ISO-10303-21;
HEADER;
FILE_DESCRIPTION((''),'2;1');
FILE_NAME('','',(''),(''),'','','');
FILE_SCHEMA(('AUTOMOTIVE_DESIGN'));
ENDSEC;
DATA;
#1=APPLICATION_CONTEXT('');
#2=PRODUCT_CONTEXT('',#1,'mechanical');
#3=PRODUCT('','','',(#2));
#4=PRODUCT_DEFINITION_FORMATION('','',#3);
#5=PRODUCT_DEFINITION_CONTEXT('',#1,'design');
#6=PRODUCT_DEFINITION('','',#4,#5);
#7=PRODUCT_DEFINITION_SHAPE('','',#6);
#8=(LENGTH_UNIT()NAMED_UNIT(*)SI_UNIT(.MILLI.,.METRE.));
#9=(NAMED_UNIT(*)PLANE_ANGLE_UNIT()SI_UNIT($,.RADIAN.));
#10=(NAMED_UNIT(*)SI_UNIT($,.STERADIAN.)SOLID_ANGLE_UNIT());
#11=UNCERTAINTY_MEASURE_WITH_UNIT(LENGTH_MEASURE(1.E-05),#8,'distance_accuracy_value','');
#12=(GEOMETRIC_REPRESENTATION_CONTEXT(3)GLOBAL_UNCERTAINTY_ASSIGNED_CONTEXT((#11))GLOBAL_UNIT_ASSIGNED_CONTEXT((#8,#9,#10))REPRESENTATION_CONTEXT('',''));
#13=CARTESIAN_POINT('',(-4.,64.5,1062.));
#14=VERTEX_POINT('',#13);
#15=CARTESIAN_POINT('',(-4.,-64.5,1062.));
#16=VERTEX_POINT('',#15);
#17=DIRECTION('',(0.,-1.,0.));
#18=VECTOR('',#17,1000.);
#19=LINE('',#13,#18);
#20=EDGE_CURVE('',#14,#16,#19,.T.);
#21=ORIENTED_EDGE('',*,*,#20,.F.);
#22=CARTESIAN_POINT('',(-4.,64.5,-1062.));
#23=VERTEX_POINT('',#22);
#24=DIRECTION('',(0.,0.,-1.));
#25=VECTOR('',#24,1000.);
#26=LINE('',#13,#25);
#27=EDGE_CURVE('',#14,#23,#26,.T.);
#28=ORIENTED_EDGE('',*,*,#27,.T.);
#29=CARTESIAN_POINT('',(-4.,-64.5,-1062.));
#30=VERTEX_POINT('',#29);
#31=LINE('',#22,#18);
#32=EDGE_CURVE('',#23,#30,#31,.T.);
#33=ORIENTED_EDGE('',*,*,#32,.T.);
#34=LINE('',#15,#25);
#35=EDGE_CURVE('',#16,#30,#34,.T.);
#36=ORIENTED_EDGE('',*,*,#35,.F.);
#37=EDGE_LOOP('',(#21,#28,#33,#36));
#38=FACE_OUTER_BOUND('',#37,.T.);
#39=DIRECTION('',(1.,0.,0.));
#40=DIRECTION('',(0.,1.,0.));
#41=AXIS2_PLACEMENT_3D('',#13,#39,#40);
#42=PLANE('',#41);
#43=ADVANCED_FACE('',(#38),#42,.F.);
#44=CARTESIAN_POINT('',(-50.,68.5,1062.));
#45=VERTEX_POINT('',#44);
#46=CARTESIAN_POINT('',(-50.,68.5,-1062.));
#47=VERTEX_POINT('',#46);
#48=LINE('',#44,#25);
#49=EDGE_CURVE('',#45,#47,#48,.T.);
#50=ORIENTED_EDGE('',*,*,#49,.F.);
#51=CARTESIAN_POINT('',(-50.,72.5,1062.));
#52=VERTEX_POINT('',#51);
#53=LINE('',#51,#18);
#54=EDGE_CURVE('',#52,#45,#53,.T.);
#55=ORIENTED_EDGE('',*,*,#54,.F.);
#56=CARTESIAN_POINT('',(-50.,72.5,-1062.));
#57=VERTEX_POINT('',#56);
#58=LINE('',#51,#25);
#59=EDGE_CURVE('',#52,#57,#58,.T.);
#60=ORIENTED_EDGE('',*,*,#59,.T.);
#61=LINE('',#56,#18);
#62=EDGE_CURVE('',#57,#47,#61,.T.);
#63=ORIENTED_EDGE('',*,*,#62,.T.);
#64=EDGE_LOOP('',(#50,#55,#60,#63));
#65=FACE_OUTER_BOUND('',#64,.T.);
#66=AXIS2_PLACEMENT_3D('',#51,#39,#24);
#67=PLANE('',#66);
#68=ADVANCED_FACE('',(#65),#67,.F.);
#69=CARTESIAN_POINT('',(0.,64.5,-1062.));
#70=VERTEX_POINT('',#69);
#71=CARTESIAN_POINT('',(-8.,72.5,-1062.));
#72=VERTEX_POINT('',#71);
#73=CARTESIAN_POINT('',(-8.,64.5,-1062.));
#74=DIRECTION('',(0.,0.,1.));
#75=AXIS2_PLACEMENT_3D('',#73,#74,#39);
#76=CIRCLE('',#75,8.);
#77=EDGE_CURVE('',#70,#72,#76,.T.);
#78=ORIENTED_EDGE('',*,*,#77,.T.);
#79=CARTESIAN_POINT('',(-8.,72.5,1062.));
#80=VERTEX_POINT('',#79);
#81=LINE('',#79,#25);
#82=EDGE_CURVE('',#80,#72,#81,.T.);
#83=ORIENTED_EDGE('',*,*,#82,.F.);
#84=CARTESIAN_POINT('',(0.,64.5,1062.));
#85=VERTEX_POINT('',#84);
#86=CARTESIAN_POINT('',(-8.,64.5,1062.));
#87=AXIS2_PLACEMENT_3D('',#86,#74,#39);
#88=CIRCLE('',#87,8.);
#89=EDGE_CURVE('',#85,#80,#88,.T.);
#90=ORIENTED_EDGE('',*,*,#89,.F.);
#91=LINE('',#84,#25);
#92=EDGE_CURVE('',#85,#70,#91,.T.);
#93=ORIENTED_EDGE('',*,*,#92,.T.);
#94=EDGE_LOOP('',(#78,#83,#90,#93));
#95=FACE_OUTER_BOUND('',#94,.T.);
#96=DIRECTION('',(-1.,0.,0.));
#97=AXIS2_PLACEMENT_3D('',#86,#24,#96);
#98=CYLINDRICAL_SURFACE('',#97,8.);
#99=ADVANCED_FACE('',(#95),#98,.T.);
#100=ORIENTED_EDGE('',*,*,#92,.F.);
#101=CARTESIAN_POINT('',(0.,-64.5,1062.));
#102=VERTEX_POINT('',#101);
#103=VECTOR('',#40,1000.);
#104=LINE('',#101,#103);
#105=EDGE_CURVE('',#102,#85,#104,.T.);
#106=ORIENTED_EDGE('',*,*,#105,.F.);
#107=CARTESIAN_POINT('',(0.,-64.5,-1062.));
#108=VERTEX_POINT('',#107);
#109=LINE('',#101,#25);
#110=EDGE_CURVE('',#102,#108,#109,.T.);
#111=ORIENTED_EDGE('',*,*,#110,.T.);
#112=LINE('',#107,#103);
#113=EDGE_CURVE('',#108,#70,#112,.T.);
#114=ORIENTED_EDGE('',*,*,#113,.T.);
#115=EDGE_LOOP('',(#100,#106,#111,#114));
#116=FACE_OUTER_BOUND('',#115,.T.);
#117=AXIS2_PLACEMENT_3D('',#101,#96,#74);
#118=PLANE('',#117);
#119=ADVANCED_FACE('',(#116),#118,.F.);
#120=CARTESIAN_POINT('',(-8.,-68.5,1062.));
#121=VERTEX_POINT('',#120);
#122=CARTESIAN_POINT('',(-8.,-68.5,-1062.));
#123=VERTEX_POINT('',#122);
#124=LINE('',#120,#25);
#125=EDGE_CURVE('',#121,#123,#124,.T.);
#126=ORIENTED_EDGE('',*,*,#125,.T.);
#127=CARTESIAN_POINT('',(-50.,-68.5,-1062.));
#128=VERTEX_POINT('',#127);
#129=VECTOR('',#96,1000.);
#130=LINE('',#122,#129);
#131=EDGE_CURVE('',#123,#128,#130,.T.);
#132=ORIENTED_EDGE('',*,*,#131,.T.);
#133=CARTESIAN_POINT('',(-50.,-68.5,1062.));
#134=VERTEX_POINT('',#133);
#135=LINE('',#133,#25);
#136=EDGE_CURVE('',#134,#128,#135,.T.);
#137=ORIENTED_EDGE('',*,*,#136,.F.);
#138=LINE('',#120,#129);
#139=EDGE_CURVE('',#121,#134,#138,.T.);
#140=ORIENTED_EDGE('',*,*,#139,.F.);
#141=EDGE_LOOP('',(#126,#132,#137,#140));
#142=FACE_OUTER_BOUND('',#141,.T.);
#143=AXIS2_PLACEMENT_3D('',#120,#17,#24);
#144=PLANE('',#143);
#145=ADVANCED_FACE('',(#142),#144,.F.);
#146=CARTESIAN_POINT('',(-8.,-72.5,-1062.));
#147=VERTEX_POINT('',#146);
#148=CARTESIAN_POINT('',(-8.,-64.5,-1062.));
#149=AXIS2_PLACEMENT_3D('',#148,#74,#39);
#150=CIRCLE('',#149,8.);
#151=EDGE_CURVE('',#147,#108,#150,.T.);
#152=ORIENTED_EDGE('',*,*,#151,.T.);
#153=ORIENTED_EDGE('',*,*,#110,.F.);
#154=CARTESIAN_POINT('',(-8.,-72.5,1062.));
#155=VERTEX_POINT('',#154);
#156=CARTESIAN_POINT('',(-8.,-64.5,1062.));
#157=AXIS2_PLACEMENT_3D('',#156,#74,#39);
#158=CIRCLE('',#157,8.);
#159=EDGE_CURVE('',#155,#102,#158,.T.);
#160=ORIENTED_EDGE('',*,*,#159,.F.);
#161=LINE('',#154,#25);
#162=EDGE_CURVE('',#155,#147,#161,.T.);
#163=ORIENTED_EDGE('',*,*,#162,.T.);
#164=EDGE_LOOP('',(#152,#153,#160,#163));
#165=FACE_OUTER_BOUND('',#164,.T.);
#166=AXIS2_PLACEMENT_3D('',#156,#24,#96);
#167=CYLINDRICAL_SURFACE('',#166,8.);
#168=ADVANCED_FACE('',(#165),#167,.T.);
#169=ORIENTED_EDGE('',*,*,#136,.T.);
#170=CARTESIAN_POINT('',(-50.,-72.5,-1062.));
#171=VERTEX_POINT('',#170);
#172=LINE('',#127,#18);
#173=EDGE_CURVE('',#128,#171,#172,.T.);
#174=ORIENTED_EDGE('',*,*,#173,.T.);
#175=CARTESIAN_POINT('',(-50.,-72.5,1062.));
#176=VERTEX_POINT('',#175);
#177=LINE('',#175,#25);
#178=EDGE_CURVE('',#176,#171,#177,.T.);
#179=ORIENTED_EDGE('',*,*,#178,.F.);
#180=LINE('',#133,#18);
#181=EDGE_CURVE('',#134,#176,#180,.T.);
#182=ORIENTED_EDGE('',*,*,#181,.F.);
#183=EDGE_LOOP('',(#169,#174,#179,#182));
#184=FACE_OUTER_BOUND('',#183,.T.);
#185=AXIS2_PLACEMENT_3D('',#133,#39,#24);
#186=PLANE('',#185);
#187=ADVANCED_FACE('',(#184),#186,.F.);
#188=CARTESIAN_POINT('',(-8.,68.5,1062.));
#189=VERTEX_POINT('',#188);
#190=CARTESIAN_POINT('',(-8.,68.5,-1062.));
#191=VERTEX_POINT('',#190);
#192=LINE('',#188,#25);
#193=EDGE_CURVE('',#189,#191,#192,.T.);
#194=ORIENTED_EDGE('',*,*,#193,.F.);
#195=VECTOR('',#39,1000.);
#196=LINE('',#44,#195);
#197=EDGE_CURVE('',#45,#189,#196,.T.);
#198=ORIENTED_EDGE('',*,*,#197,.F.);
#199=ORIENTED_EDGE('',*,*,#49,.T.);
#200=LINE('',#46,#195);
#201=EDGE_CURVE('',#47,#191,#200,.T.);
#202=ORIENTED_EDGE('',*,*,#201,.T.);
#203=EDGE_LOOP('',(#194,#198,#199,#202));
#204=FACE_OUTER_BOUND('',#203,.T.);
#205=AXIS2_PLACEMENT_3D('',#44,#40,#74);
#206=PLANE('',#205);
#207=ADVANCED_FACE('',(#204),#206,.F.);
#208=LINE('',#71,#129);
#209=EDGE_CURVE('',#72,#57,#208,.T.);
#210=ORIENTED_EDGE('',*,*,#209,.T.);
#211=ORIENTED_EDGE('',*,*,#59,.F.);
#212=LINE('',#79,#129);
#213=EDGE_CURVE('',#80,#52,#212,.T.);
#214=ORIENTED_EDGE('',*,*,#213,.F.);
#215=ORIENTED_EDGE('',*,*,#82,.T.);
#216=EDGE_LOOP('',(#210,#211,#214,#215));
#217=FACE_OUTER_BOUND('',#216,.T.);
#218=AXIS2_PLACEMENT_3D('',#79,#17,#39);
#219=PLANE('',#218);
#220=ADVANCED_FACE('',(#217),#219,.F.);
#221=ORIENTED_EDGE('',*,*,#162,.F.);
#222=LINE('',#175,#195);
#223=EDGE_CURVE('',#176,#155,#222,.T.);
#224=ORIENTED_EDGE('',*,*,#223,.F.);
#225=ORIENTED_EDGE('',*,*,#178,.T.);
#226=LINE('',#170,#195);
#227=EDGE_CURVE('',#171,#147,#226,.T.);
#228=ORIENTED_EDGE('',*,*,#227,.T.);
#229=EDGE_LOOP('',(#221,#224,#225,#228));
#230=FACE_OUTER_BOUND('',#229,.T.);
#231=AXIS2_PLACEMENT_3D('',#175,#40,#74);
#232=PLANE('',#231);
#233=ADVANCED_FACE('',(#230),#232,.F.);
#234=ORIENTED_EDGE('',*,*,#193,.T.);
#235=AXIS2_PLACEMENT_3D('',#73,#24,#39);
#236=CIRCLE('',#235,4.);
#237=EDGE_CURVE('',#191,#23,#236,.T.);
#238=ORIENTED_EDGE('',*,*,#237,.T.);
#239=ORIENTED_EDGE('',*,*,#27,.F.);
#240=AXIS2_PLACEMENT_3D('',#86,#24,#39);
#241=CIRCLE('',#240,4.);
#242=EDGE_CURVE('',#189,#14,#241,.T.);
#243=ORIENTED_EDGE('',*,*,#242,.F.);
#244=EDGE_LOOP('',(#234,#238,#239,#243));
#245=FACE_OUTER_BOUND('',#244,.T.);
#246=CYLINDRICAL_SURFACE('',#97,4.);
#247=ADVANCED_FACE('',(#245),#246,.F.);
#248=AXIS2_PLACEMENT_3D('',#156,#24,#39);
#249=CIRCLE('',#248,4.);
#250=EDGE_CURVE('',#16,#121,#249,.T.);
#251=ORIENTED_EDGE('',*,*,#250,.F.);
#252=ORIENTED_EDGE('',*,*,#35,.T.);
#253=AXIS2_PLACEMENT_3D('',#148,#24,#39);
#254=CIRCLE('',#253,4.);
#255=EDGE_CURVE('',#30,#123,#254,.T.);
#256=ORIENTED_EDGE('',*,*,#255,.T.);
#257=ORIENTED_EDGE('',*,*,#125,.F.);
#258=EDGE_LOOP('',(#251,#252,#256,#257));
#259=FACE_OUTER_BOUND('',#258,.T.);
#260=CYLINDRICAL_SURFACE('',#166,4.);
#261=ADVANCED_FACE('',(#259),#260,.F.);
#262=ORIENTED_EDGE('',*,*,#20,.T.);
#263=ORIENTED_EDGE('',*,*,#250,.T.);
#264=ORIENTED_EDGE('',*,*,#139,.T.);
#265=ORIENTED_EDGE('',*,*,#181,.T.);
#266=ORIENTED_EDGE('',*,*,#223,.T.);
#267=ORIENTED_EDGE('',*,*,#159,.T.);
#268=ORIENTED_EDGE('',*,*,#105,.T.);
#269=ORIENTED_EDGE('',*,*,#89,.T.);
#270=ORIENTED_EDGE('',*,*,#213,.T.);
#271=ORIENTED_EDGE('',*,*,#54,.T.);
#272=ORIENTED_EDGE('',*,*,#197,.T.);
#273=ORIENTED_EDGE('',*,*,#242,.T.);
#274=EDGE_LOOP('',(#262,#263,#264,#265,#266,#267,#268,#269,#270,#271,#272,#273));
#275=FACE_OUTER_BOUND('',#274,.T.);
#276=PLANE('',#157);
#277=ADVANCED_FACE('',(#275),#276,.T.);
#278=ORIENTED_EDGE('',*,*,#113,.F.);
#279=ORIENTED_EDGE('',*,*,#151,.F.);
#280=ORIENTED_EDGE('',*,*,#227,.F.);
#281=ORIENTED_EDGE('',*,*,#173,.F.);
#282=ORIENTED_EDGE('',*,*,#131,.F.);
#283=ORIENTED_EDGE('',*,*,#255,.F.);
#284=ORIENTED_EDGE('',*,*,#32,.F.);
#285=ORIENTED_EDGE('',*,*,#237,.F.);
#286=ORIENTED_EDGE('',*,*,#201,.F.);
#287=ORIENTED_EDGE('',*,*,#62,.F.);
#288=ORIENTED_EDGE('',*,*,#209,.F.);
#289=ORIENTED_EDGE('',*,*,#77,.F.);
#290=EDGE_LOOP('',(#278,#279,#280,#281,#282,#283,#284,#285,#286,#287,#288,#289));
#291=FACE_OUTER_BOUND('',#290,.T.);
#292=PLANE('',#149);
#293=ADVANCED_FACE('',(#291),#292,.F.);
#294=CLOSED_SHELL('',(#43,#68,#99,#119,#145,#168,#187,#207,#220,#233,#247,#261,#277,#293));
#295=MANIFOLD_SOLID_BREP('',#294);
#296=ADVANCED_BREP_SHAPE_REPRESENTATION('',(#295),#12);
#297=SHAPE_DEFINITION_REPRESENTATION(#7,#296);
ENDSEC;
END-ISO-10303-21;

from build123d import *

# Parameters (mm, degrees)
BOSS_EXTRUDE1_DEPTH = 1062


with BuildPart() as part:
    # Sketch1 → Boss-Extrude1 (new, symmetric)
    with BuildSketch(Plane.XY):
        with BuildLine():
            Line((-50, -72.5), (-8, -72.5))
            ThreePointArc((-8, -72.5), (-2.343145751, -70.156854249), (0, -64.5))
            Line((0, -64.5), (0, 64.5))
            ThreePointArc((0, 64.5), (-2.343145751, 70.156854249), (-8, 72.5))
            Line((-8, 72.5), (-50, 72.5))
            Line((-50, 72.5), (-50, 68.5))
            Line((-50, 68.5), (-8, 68.5))
            ThreePointArc((-8, 68.5), (-5.171572875, 67.328427125), (-4, 64.5))
            Line((-4, 64.5), (-4, -64.5))
            ThreePointArc((-4, -64.5), (-5.171572875, -67.328427125), (-8, -68.5))
            Line((-8, -68.5), (-50, -68.5))
            Line((-50, -68.5), (-50, -72.5))
        make_face()
    extrude(amount=BOSS_EXTRUDE1_DEPTH, both=True)


solid = part.part
